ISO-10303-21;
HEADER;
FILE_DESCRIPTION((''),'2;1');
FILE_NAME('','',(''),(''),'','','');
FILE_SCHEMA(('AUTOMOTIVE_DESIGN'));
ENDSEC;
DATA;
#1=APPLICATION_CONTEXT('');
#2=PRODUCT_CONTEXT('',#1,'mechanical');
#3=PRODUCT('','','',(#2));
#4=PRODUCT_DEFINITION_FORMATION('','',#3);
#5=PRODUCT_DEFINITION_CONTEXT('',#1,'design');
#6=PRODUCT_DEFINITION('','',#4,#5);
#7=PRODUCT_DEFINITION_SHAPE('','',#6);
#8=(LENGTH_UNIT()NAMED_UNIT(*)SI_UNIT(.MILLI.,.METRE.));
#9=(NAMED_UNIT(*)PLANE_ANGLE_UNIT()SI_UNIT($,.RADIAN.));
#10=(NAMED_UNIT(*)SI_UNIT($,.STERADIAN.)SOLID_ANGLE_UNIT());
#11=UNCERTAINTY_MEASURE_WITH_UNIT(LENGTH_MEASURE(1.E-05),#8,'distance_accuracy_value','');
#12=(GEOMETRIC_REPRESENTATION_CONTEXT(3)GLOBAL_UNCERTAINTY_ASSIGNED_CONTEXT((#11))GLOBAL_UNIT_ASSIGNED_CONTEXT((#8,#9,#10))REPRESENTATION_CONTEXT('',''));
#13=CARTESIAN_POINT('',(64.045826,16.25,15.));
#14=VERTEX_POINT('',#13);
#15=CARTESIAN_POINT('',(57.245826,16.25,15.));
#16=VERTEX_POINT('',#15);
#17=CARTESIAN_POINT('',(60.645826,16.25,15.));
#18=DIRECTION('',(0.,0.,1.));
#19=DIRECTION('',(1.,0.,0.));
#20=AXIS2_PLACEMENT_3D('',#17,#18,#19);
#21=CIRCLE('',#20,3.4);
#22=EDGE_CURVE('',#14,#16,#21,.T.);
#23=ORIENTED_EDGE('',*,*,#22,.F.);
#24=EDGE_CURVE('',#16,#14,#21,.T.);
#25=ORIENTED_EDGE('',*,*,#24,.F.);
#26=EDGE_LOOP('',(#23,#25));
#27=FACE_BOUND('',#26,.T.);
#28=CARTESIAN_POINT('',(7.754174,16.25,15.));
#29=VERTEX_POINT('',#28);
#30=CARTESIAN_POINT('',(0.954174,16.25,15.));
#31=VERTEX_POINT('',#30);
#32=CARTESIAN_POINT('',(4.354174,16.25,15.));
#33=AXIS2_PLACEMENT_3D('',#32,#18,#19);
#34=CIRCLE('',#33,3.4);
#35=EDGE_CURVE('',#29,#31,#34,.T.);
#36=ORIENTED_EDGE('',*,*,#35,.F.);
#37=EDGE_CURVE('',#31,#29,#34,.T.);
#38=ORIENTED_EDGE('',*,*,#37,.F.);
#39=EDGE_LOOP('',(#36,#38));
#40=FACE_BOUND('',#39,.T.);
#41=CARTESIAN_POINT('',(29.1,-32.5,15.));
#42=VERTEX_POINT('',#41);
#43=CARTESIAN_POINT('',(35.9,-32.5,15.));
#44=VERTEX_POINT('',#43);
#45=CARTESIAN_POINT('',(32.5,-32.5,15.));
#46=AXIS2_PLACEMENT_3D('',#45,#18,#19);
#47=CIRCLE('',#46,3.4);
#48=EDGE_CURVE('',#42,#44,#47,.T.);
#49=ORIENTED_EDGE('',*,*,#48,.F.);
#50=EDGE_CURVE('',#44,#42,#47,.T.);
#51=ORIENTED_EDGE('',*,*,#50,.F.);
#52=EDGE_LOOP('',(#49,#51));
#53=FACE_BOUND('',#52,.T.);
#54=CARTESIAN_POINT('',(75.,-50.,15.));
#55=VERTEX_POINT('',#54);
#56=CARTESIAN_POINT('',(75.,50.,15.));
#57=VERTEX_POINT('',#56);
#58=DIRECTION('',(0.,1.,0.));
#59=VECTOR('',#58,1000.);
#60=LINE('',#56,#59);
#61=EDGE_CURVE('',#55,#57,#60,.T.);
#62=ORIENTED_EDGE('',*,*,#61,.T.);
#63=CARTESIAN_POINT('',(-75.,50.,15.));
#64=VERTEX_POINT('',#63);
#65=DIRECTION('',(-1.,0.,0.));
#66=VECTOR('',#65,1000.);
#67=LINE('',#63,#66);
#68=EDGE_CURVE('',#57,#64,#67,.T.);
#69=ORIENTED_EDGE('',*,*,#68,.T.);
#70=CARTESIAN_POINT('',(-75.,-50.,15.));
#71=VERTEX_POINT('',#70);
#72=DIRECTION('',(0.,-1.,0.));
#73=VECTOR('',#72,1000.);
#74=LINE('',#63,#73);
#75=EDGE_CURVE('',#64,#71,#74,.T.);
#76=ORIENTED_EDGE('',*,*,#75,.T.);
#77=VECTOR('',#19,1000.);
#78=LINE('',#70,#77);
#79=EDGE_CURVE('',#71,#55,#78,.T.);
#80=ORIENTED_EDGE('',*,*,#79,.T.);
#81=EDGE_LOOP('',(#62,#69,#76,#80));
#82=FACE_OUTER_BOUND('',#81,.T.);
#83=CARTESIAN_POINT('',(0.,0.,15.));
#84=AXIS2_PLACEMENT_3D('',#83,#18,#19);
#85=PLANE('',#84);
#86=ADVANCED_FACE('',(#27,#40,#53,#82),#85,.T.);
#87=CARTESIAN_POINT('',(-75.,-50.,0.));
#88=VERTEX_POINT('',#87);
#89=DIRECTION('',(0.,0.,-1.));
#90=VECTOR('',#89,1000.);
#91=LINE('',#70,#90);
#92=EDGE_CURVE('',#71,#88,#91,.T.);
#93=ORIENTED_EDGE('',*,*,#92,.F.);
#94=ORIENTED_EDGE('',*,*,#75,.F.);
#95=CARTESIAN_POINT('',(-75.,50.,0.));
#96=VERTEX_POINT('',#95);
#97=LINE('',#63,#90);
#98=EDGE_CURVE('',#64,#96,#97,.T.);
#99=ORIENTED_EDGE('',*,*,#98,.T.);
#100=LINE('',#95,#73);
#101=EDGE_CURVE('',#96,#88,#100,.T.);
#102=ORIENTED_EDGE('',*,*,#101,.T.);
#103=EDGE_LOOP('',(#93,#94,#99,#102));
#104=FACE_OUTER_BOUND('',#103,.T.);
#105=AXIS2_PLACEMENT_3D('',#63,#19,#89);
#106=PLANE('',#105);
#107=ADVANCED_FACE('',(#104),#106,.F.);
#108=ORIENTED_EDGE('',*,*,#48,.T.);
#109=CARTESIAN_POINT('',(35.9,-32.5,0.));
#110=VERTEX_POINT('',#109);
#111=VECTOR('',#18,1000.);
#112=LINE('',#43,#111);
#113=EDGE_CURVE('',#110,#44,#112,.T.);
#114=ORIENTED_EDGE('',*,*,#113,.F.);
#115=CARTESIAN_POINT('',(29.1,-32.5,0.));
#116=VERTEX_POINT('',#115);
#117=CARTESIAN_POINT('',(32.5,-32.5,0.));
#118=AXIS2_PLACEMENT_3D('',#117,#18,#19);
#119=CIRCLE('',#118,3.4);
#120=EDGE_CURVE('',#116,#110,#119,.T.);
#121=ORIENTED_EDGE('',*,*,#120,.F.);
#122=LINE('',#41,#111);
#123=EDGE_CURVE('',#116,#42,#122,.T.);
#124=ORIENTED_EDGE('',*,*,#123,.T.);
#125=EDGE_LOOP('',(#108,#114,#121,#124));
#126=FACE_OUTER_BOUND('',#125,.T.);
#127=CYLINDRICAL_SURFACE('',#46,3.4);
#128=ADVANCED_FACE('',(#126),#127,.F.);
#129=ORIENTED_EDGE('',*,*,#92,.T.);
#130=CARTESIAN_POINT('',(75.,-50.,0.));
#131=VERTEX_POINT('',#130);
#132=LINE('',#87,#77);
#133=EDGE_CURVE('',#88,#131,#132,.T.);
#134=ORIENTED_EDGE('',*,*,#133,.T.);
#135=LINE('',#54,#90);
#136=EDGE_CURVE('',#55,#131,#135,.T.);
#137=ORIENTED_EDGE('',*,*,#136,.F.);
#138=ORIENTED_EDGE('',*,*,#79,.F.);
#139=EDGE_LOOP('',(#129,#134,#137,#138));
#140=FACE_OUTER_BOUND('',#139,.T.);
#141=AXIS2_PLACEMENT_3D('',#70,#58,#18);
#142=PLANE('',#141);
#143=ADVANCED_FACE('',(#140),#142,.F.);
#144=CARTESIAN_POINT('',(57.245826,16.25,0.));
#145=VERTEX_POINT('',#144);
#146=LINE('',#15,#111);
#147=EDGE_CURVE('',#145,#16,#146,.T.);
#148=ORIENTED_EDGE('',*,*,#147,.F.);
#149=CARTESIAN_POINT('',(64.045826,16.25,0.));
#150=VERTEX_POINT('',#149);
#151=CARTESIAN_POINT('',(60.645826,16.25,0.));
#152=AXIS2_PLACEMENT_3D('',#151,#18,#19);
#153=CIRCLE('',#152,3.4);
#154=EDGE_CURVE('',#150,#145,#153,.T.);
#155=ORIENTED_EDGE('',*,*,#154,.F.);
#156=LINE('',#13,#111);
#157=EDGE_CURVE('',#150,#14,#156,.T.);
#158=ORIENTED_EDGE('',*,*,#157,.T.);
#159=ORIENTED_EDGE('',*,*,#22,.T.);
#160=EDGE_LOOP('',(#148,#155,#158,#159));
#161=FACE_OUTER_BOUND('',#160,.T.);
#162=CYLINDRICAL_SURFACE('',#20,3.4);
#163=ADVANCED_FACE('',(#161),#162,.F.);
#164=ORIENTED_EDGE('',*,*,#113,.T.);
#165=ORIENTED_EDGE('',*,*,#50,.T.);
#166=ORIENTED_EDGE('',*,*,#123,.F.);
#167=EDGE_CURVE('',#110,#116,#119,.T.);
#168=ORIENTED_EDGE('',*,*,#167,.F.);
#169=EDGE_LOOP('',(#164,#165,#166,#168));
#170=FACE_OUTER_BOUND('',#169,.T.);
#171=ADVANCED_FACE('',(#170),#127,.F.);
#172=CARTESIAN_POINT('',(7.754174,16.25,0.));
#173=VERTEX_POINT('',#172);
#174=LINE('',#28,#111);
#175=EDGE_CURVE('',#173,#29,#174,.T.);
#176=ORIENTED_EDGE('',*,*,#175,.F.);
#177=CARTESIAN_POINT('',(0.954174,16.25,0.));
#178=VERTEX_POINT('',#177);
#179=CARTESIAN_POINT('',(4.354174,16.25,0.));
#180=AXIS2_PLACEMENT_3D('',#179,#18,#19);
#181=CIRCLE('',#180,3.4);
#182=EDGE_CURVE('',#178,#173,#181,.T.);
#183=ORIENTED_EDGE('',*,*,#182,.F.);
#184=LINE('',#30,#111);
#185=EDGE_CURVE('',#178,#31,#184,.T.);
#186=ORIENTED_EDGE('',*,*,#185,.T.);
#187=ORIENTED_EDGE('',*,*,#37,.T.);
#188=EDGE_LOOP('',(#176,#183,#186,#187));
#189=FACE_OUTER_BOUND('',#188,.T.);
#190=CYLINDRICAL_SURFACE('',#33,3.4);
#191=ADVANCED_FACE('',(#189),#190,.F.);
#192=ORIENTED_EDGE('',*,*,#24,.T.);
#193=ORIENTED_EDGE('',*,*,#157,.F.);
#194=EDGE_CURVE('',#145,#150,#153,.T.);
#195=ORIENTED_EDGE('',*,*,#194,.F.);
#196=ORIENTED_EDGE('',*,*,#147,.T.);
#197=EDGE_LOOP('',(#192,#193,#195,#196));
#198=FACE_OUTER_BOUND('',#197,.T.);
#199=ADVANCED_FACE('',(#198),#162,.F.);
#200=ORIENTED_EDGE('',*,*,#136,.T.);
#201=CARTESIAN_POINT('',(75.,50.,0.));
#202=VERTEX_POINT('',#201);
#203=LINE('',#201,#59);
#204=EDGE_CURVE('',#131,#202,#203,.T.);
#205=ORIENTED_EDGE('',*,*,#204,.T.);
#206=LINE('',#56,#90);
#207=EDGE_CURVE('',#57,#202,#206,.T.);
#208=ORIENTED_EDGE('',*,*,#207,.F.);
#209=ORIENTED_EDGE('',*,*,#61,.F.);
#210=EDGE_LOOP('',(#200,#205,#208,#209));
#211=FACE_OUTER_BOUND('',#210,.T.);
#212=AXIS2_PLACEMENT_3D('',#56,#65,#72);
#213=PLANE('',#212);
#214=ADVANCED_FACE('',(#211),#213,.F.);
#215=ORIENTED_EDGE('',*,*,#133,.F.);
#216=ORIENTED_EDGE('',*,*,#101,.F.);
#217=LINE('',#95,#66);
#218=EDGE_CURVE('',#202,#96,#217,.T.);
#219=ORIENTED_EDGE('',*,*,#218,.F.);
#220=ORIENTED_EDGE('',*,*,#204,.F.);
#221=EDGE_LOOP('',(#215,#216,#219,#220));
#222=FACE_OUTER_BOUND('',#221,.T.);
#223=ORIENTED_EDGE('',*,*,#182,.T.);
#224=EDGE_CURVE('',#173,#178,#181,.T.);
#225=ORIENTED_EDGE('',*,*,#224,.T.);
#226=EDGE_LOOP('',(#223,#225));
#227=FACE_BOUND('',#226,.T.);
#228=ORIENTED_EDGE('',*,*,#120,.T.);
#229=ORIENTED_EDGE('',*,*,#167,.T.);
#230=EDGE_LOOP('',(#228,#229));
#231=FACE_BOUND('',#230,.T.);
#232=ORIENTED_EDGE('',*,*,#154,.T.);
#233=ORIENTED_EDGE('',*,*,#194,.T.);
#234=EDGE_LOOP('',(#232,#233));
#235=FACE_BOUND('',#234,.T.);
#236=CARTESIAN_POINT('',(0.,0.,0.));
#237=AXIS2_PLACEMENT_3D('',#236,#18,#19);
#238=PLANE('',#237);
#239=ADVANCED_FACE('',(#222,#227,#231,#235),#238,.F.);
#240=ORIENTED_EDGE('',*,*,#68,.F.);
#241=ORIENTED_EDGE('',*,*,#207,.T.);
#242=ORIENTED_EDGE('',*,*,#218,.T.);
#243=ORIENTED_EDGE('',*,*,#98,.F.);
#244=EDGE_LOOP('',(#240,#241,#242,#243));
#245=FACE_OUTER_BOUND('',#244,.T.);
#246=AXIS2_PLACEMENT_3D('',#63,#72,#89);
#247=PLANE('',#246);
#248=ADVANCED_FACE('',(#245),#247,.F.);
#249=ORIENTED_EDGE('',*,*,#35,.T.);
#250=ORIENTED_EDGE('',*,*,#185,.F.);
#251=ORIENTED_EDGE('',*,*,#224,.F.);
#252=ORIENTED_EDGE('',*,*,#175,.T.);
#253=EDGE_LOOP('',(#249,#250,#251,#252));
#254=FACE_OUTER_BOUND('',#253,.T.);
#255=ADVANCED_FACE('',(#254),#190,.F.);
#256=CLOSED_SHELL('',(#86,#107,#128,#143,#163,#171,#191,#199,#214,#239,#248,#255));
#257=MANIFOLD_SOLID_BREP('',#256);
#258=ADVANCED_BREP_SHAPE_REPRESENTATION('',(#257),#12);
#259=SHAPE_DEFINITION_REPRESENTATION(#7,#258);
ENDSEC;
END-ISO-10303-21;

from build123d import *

# Parameters (mm, degrees)
SKETCH1_W             = 150
SKETCH1_H             = 100
BOSS_EXTRUDE1_DEPTH   = 15
M8_TAPPED_HOLE1_D     = 6.8
M8_TAPPED_HOLE1_DEPTH = 19.75
M8_TAPPED_HOLE1_TIP   = 2.042926105


with BuildPart() as part:
    # Sketch1 → Boss-Extrude1 (new body)
    with BuildSketch(Plane.XY):
        Rectangle(SKETCH1_W, SKETCH1_H)
    extrude(amount=BOSS_EXTRUDE1_DEPTH)

    # M8 Tapped Hole1
    with Locations(Plane.XY.offset(15)):
        with Locations((4.354174377, 16.25), (60.645825623, 16.25), (32.5, -32.5)):
            Hole(M8_TAPPED_HOLE1_D / 2, depth=M8_TAPPED_HOLE1_DEPTH)
            with Locations((0, 0, -(M8_TAPPED_HOLE1_DEPTH + M8_TAPPED_HOLE1_TIP / 2))):  # 118° drill point
                Cone(0, M8_TAPPED_HOLE1_D / 2, M8_TAPPED_HOLE1_TIP, mode=Mode.SUBTRACT)


solid = part.part
